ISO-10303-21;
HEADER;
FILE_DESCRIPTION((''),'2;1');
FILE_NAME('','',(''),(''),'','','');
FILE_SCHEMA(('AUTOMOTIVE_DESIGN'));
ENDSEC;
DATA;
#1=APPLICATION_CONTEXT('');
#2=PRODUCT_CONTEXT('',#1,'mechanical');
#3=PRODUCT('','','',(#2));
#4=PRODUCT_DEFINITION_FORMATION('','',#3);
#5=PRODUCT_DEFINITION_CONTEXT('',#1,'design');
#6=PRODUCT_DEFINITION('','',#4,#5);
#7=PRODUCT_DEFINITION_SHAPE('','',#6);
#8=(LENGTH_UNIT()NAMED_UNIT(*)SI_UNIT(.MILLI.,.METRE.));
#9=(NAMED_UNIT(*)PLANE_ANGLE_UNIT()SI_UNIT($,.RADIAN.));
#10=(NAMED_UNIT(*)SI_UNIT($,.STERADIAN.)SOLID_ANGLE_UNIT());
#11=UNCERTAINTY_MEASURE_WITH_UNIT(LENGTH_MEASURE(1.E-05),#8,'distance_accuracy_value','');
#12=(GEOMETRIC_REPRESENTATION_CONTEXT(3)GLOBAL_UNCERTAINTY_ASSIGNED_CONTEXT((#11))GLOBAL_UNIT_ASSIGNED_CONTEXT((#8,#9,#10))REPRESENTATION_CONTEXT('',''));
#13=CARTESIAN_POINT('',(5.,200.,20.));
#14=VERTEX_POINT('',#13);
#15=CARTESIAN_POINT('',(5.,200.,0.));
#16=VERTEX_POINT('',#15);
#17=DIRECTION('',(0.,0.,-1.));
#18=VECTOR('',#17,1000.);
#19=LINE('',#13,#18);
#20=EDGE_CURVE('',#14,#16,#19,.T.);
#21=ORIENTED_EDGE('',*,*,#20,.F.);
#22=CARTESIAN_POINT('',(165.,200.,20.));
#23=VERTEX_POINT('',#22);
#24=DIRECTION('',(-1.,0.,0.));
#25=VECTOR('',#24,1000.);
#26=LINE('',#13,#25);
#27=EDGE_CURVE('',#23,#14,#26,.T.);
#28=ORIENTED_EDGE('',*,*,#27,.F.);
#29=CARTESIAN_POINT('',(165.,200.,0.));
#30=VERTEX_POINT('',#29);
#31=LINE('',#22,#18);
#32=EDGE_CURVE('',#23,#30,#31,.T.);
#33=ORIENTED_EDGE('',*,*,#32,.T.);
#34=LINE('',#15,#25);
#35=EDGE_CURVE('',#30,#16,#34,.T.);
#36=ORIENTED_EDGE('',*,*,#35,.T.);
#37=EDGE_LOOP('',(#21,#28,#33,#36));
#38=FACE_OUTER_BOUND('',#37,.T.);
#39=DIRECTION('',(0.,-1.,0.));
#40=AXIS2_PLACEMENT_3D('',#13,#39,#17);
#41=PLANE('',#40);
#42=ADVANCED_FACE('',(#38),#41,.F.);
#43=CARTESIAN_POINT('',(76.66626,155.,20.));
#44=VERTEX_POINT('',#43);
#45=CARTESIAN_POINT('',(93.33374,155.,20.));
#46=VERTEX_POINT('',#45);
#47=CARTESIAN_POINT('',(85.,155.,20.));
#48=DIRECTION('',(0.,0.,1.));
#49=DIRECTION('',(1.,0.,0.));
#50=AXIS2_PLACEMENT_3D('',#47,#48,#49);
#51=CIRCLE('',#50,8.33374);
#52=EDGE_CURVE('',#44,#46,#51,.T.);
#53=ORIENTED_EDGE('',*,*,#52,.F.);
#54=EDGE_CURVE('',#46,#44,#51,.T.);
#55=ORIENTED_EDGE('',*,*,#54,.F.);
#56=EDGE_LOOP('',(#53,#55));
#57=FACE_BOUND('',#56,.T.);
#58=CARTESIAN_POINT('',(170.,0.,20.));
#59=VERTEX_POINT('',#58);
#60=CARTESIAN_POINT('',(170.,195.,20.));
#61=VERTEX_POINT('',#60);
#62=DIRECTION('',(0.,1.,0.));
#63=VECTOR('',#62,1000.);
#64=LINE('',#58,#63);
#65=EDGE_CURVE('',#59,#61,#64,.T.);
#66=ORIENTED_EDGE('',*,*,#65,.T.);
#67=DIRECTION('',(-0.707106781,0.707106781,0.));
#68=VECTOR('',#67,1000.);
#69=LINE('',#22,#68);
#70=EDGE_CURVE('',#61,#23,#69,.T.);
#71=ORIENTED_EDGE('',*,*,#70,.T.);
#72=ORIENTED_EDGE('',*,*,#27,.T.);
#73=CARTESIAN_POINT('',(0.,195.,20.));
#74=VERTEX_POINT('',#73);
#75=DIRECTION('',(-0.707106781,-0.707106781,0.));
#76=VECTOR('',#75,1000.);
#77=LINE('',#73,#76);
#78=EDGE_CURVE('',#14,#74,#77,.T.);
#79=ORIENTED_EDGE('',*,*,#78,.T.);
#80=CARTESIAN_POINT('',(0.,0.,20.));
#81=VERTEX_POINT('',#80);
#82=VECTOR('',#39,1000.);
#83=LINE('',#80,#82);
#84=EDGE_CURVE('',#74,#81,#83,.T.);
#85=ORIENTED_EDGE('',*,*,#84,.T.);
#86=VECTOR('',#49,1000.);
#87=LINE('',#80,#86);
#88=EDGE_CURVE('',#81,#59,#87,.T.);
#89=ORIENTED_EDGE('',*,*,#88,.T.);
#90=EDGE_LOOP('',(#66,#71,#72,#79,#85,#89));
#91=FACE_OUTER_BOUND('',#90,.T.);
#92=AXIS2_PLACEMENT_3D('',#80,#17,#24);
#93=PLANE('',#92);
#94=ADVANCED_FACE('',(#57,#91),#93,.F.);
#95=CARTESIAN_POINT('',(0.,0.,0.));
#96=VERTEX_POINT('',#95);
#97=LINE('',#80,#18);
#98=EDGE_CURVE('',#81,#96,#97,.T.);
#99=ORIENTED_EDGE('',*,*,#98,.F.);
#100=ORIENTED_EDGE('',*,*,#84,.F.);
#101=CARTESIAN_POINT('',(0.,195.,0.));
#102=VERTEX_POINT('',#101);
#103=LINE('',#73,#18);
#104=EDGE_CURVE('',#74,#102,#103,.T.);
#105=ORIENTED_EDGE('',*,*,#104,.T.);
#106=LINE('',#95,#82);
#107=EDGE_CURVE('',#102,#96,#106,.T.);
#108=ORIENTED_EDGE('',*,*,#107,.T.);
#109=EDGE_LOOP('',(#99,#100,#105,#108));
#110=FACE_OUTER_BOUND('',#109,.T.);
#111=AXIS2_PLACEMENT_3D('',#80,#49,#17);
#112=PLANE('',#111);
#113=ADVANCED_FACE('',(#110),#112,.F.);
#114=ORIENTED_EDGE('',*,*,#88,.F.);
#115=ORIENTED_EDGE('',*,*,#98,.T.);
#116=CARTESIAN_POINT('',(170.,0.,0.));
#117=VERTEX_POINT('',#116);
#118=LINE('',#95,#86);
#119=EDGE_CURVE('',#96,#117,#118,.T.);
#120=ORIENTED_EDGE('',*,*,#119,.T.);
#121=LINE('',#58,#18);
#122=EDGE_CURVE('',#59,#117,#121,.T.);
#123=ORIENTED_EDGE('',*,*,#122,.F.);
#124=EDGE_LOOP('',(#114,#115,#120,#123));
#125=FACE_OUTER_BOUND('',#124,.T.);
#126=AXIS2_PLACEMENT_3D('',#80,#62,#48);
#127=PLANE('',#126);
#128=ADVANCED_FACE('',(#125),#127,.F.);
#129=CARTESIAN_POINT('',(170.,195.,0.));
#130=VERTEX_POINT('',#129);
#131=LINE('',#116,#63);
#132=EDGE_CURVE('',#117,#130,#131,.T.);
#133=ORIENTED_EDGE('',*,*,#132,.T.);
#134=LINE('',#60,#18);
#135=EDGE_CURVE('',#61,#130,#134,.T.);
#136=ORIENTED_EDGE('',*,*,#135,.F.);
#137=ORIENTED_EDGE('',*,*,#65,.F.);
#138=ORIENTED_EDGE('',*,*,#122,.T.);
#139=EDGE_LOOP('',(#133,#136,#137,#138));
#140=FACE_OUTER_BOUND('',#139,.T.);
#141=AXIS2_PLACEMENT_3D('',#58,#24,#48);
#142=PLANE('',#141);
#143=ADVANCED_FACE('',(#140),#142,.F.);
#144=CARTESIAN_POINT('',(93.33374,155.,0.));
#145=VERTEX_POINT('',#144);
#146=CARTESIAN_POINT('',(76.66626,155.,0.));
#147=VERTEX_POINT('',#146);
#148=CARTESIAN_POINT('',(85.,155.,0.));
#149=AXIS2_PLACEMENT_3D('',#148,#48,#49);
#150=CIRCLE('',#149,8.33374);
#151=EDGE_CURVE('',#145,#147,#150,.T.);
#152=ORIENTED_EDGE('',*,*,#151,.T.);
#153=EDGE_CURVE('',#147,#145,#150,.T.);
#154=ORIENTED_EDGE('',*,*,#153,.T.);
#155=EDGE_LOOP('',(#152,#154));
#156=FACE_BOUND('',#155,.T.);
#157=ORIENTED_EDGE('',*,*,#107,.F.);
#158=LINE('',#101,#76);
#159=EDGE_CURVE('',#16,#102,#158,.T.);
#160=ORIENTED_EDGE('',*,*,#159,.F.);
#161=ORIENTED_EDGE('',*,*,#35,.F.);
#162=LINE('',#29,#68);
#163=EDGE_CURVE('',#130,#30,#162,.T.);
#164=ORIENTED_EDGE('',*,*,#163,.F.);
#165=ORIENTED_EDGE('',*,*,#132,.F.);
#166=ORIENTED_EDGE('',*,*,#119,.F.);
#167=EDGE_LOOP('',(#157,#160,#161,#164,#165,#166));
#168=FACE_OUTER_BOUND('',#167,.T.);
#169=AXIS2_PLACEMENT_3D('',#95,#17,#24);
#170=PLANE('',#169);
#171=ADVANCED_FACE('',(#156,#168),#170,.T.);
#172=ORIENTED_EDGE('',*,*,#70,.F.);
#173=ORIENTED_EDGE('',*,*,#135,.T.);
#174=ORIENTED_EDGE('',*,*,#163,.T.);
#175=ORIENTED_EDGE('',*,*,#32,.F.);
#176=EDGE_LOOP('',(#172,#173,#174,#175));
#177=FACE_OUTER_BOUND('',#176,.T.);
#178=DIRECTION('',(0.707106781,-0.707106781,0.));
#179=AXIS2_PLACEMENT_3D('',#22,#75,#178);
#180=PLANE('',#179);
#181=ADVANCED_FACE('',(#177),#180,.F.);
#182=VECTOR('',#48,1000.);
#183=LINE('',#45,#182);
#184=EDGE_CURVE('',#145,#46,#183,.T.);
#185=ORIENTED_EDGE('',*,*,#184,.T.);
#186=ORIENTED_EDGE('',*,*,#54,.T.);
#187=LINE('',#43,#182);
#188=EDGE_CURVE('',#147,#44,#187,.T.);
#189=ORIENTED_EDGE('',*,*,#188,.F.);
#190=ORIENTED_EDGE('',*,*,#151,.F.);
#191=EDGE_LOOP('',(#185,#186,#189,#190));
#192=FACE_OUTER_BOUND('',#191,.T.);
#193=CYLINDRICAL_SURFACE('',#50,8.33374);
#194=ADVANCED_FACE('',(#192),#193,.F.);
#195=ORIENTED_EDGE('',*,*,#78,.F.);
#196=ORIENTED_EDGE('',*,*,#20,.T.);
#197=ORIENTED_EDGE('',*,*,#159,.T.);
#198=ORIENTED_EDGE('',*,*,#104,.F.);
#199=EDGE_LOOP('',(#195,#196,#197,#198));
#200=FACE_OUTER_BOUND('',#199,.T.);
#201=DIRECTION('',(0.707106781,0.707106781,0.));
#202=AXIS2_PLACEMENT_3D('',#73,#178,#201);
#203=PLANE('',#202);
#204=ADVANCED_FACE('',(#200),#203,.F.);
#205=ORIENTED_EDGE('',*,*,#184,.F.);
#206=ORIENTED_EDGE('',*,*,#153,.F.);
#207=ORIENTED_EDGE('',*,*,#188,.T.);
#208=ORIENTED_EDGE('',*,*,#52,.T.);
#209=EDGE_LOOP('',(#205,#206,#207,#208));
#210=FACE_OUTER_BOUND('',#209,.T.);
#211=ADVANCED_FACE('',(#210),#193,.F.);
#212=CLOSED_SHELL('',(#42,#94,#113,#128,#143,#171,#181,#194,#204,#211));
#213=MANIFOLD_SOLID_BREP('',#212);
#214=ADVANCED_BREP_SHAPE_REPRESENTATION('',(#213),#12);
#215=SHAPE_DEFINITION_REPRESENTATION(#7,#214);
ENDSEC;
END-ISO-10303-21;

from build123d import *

# Parameters (mm, degrees)
BOSS_EXTRUDE1_DEPTH     = 20
F_3_4_10_TAPPED_HOLE1_D = 16.66748


with BuildPart() as part:
    # Sketch1 → Boss-Extrude1 (new body)
    with BuildSketch(Plane.XY):
        Polygon((0, 195), (5, 200), (165, 200), (170, 195), (170, 0), (0, 0), align=None)
    extrude(amount=BOSS_EXTRUDE1_DEPTH)

    # 3/4-10 Tapped Hole1 (through all)
    with Locations(Plane(origin=(85, 155, 20), x_dir=(1, 0, 0), z_dir=(0, 0, 1))):
        with Locations((0, 0)):
            Hole(F_3_4_10_TAPPED_HOLE1_D / 2)


solid = part.part
